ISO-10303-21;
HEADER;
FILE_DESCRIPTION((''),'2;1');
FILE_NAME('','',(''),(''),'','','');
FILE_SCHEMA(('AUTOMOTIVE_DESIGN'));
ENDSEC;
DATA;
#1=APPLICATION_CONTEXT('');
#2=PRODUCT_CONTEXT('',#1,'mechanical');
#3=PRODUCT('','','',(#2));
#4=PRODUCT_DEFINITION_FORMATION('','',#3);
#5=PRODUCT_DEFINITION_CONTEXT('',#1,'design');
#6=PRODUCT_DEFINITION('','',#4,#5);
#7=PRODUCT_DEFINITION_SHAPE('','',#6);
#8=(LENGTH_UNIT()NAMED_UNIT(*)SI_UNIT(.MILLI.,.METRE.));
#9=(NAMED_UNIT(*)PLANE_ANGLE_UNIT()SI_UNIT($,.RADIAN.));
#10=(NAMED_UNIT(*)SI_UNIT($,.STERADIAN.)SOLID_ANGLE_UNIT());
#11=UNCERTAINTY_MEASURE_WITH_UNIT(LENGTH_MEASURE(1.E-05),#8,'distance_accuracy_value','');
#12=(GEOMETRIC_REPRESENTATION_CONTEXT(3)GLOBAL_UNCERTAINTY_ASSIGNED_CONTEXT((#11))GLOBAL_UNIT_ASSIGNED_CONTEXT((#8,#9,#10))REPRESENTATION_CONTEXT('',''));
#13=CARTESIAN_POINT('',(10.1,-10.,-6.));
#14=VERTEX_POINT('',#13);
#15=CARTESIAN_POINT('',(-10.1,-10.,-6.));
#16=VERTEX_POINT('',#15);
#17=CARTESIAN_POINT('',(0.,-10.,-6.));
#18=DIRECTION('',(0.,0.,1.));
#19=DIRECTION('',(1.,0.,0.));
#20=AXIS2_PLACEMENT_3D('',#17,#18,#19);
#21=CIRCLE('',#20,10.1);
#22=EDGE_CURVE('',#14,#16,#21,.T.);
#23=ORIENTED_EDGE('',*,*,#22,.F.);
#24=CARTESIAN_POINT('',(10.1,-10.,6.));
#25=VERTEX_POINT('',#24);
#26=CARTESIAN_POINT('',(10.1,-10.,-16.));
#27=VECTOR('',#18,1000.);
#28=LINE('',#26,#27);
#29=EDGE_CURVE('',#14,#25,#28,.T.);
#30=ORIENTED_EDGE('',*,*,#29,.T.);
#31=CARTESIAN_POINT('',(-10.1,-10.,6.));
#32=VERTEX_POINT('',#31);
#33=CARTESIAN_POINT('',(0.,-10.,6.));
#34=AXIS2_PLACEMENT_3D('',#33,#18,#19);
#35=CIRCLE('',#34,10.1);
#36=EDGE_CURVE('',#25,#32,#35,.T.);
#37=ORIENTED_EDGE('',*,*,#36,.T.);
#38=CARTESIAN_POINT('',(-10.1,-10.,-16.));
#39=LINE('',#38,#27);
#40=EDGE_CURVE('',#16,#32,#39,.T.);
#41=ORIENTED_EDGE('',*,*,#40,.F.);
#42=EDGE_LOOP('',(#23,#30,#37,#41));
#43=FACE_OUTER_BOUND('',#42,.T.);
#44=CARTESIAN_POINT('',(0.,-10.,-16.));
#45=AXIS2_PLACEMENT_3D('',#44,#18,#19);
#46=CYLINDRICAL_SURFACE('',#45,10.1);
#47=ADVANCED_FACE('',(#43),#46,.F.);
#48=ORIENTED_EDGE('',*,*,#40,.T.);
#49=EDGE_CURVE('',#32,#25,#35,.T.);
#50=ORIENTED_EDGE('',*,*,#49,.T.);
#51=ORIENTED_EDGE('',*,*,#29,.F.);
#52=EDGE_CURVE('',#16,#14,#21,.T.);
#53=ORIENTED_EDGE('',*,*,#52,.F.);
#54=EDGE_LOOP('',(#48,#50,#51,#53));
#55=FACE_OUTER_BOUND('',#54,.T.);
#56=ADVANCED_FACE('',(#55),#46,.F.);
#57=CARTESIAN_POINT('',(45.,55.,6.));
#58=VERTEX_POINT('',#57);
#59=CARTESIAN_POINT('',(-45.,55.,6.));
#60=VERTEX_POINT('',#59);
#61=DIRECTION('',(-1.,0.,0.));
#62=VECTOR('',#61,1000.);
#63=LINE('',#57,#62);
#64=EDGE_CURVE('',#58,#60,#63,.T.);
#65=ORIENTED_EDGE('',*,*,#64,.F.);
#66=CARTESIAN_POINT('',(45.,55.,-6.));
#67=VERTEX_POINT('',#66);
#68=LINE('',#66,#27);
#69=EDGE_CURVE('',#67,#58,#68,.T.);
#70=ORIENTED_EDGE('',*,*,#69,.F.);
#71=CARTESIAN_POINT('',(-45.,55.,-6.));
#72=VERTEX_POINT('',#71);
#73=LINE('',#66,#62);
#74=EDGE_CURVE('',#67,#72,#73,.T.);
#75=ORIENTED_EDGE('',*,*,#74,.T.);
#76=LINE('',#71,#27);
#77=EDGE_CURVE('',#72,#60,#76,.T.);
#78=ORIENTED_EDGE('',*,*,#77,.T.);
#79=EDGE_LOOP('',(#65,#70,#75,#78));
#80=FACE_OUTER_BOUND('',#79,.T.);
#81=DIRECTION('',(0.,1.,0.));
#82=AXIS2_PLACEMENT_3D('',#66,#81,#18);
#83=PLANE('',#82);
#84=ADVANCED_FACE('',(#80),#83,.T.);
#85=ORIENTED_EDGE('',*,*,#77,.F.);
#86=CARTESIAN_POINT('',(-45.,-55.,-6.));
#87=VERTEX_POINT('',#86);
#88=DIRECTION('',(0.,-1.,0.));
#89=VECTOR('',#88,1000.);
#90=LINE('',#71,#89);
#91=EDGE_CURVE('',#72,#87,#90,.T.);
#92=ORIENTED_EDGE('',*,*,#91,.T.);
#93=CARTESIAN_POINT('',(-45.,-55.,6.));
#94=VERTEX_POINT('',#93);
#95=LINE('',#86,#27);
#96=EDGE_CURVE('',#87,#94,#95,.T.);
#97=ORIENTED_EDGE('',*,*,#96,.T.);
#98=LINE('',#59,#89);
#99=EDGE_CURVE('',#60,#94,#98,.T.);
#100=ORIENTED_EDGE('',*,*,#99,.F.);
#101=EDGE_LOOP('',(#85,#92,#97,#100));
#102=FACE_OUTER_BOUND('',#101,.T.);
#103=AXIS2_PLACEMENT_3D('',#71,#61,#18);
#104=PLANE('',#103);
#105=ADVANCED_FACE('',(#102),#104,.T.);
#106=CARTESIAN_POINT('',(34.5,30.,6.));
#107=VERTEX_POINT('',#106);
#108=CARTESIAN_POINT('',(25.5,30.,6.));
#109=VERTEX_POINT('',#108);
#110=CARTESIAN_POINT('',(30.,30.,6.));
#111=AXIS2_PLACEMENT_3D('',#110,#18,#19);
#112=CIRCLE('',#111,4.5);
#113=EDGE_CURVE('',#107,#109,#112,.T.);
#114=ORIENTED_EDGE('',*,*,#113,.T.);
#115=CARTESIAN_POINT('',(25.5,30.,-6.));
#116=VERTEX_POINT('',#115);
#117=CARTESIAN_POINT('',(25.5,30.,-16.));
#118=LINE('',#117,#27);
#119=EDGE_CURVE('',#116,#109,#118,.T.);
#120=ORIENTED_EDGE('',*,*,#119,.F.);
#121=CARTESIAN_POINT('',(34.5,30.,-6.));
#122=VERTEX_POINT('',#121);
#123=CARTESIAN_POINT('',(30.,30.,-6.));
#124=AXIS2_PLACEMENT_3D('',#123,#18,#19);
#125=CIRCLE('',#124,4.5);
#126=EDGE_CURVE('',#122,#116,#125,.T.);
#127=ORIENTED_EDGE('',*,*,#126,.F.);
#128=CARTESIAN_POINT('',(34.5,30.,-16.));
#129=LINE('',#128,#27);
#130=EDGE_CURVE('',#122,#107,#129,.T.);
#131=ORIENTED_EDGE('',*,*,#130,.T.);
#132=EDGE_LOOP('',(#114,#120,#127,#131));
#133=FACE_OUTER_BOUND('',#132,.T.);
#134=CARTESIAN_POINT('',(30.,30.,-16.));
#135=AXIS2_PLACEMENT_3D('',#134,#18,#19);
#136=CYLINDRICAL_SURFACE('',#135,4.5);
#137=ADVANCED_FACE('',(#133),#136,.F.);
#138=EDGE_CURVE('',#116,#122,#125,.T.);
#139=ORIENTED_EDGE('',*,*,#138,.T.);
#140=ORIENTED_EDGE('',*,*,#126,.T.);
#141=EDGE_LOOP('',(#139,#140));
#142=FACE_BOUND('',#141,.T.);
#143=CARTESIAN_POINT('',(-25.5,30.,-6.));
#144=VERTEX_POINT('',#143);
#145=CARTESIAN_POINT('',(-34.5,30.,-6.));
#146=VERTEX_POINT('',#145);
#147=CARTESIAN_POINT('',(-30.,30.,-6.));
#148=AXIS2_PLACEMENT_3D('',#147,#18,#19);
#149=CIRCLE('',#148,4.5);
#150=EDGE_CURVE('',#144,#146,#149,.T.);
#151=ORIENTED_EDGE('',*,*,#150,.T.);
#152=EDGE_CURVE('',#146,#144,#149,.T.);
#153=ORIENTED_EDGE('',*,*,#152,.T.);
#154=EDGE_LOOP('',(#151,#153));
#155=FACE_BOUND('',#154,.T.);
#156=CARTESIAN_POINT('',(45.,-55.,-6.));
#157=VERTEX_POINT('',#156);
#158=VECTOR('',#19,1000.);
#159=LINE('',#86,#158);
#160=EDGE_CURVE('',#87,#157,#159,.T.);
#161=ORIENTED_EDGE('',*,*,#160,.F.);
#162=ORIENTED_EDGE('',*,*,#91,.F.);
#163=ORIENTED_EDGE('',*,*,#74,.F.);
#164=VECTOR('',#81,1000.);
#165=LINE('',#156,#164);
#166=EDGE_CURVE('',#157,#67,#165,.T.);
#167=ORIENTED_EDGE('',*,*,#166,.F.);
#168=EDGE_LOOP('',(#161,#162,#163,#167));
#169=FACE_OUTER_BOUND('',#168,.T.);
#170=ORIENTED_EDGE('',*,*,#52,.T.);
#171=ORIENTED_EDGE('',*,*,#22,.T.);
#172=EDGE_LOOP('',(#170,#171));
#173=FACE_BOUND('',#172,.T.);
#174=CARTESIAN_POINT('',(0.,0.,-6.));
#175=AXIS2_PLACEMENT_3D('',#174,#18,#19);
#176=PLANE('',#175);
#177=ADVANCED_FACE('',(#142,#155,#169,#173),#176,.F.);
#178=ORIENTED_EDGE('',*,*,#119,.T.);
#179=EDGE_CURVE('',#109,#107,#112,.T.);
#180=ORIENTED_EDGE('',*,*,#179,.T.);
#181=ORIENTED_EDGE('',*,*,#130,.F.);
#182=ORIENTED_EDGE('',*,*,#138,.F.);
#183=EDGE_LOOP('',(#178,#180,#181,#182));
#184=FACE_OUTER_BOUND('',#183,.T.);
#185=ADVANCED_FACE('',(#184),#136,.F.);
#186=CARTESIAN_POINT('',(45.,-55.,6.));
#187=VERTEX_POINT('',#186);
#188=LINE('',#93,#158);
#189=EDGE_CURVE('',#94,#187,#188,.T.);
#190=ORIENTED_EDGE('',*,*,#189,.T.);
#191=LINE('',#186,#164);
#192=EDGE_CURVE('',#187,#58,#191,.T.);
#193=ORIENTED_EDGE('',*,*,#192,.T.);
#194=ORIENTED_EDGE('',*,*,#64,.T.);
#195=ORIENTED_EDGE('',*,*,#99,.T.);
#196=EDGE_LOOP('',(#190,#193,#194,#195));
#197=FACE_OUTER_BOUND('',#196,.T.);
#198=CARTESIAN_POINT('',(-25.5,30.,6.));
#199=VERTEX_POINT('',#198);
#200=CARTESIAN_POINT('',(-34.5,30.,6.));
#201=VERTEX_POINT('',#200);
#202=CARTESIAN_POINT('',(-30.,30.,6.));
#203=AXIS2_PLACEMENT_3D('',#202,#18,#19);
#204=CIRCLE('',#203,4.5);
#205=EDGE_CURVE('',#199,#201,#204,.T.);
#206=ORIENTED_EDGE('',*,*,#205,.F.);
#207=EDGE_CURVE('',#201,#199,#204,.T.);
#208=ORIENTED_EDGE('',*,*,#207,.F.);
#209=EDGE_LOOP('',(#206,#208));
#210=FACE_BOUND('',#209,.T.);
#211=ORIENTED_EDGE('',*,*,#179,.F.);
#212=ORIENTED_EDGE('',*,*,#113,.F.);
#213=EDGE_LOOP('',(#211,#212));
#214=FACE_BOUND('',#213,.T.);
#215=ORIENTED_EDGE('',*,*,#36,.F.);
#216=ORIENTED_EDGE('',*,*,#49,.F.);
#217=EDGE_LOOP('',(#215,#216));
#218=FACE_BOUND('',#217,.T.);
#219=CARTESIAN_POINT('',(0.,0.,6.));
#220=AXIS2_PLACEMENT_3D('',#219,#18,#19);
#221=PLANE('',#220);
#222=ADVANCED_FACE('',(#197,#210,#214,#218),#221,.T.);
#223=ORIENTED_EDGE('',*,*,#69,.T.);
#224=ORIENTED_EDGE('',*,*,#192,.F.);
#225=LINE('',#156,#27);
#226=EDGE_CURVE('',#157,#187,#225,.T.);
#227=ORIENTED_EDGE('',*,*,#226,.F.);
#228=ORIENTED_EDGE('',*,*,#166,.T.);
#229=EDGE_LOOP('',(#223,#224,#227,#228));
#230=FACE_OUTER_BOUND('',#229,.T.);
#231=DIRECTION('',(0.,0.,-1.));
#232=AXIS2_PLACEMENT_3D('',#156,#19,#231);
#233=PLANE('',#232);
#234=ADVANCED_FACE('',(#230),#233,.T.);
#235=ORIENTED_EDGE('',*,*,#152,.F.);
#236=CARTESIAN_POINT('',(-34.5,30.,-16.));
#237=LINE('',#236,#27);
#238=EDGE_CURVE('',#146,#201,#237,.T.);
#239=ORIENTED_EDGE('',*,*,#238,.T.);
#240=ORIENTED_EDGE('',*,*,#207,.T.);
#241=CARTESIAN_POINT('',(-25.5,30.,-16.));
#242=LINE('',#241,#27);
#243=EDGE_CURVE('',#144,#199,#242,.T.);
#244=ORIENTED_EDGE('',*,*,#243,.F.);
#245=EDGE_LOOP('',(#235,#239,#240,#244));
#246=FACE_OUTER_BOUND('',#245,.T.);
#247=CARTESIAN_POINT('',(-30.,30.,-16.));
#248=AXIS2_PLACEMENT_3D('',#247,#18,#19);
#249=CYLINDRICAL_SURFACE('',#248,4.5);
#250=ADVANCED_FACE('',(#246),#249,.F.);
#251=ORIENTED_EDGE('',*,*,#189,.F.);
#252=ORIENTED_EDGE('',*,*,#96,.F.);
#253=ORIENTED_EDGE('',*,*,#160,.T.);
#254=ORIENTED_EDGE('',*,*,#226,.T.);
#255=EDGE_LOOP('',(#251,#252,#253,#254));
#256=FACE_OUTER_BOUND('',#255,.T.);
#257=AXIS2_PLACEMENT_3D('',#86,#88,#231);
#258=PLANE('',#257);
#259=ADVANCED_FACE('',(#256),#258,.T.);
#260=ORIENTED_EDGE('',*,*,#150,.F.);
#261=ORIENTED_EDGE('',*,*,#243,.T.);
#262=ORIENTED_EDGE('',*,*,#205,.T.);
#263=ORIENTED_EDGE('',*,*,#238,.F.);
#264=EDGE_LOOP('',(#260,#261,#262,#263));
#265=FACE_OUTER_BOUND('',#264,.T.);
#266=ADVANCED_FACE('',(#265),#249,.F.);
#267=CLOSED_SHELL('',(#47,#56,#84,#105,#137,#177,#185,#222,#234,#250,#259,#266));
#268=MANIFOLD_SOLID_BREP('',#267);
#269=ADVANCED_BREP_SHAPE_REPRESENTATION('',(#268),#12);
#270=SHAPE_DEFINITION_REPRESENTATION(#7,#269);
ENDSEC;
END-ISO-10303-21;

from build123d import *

# Parameters (mm, degrees)
SKETCH_1_W          = 90
SKETCH_1_H          = 110
EXTRUDE_1_DEPTH     = 6
SKETCH_2_R          = 4.5
SKETCH_2_R_2        = 10.1
CUT_EXTRUDE_1_DEPTH = 16


with BuildPart() as part:
    # 草图1 → 凸台-拉伸1 (new, symmetric)
    with BuildSketch(Plane.XY):
        Rectangle(SKETCH_1_W, SKETCH_1_H)
    extrude(amount=EXTRUDE_1_DEPTH, both=True)

    # 草图2 → 切除-拉伸1 (cut, symmetric)
    with BuildSketch(Plane.XY):
        with Locations((-30, 30)):
            Circle(SKETCH_2_R)
        with Locations((30, 30)):
            Circle(SKETCH_2_R)
        with Locations((0, -10)):
            Circle(SKETCH_2_R_2)
    extrude(amount=CUT_EXTRUDE_1_DEPTH, both=True, mode=Mode.SUBTRACT)


solid = part.part
